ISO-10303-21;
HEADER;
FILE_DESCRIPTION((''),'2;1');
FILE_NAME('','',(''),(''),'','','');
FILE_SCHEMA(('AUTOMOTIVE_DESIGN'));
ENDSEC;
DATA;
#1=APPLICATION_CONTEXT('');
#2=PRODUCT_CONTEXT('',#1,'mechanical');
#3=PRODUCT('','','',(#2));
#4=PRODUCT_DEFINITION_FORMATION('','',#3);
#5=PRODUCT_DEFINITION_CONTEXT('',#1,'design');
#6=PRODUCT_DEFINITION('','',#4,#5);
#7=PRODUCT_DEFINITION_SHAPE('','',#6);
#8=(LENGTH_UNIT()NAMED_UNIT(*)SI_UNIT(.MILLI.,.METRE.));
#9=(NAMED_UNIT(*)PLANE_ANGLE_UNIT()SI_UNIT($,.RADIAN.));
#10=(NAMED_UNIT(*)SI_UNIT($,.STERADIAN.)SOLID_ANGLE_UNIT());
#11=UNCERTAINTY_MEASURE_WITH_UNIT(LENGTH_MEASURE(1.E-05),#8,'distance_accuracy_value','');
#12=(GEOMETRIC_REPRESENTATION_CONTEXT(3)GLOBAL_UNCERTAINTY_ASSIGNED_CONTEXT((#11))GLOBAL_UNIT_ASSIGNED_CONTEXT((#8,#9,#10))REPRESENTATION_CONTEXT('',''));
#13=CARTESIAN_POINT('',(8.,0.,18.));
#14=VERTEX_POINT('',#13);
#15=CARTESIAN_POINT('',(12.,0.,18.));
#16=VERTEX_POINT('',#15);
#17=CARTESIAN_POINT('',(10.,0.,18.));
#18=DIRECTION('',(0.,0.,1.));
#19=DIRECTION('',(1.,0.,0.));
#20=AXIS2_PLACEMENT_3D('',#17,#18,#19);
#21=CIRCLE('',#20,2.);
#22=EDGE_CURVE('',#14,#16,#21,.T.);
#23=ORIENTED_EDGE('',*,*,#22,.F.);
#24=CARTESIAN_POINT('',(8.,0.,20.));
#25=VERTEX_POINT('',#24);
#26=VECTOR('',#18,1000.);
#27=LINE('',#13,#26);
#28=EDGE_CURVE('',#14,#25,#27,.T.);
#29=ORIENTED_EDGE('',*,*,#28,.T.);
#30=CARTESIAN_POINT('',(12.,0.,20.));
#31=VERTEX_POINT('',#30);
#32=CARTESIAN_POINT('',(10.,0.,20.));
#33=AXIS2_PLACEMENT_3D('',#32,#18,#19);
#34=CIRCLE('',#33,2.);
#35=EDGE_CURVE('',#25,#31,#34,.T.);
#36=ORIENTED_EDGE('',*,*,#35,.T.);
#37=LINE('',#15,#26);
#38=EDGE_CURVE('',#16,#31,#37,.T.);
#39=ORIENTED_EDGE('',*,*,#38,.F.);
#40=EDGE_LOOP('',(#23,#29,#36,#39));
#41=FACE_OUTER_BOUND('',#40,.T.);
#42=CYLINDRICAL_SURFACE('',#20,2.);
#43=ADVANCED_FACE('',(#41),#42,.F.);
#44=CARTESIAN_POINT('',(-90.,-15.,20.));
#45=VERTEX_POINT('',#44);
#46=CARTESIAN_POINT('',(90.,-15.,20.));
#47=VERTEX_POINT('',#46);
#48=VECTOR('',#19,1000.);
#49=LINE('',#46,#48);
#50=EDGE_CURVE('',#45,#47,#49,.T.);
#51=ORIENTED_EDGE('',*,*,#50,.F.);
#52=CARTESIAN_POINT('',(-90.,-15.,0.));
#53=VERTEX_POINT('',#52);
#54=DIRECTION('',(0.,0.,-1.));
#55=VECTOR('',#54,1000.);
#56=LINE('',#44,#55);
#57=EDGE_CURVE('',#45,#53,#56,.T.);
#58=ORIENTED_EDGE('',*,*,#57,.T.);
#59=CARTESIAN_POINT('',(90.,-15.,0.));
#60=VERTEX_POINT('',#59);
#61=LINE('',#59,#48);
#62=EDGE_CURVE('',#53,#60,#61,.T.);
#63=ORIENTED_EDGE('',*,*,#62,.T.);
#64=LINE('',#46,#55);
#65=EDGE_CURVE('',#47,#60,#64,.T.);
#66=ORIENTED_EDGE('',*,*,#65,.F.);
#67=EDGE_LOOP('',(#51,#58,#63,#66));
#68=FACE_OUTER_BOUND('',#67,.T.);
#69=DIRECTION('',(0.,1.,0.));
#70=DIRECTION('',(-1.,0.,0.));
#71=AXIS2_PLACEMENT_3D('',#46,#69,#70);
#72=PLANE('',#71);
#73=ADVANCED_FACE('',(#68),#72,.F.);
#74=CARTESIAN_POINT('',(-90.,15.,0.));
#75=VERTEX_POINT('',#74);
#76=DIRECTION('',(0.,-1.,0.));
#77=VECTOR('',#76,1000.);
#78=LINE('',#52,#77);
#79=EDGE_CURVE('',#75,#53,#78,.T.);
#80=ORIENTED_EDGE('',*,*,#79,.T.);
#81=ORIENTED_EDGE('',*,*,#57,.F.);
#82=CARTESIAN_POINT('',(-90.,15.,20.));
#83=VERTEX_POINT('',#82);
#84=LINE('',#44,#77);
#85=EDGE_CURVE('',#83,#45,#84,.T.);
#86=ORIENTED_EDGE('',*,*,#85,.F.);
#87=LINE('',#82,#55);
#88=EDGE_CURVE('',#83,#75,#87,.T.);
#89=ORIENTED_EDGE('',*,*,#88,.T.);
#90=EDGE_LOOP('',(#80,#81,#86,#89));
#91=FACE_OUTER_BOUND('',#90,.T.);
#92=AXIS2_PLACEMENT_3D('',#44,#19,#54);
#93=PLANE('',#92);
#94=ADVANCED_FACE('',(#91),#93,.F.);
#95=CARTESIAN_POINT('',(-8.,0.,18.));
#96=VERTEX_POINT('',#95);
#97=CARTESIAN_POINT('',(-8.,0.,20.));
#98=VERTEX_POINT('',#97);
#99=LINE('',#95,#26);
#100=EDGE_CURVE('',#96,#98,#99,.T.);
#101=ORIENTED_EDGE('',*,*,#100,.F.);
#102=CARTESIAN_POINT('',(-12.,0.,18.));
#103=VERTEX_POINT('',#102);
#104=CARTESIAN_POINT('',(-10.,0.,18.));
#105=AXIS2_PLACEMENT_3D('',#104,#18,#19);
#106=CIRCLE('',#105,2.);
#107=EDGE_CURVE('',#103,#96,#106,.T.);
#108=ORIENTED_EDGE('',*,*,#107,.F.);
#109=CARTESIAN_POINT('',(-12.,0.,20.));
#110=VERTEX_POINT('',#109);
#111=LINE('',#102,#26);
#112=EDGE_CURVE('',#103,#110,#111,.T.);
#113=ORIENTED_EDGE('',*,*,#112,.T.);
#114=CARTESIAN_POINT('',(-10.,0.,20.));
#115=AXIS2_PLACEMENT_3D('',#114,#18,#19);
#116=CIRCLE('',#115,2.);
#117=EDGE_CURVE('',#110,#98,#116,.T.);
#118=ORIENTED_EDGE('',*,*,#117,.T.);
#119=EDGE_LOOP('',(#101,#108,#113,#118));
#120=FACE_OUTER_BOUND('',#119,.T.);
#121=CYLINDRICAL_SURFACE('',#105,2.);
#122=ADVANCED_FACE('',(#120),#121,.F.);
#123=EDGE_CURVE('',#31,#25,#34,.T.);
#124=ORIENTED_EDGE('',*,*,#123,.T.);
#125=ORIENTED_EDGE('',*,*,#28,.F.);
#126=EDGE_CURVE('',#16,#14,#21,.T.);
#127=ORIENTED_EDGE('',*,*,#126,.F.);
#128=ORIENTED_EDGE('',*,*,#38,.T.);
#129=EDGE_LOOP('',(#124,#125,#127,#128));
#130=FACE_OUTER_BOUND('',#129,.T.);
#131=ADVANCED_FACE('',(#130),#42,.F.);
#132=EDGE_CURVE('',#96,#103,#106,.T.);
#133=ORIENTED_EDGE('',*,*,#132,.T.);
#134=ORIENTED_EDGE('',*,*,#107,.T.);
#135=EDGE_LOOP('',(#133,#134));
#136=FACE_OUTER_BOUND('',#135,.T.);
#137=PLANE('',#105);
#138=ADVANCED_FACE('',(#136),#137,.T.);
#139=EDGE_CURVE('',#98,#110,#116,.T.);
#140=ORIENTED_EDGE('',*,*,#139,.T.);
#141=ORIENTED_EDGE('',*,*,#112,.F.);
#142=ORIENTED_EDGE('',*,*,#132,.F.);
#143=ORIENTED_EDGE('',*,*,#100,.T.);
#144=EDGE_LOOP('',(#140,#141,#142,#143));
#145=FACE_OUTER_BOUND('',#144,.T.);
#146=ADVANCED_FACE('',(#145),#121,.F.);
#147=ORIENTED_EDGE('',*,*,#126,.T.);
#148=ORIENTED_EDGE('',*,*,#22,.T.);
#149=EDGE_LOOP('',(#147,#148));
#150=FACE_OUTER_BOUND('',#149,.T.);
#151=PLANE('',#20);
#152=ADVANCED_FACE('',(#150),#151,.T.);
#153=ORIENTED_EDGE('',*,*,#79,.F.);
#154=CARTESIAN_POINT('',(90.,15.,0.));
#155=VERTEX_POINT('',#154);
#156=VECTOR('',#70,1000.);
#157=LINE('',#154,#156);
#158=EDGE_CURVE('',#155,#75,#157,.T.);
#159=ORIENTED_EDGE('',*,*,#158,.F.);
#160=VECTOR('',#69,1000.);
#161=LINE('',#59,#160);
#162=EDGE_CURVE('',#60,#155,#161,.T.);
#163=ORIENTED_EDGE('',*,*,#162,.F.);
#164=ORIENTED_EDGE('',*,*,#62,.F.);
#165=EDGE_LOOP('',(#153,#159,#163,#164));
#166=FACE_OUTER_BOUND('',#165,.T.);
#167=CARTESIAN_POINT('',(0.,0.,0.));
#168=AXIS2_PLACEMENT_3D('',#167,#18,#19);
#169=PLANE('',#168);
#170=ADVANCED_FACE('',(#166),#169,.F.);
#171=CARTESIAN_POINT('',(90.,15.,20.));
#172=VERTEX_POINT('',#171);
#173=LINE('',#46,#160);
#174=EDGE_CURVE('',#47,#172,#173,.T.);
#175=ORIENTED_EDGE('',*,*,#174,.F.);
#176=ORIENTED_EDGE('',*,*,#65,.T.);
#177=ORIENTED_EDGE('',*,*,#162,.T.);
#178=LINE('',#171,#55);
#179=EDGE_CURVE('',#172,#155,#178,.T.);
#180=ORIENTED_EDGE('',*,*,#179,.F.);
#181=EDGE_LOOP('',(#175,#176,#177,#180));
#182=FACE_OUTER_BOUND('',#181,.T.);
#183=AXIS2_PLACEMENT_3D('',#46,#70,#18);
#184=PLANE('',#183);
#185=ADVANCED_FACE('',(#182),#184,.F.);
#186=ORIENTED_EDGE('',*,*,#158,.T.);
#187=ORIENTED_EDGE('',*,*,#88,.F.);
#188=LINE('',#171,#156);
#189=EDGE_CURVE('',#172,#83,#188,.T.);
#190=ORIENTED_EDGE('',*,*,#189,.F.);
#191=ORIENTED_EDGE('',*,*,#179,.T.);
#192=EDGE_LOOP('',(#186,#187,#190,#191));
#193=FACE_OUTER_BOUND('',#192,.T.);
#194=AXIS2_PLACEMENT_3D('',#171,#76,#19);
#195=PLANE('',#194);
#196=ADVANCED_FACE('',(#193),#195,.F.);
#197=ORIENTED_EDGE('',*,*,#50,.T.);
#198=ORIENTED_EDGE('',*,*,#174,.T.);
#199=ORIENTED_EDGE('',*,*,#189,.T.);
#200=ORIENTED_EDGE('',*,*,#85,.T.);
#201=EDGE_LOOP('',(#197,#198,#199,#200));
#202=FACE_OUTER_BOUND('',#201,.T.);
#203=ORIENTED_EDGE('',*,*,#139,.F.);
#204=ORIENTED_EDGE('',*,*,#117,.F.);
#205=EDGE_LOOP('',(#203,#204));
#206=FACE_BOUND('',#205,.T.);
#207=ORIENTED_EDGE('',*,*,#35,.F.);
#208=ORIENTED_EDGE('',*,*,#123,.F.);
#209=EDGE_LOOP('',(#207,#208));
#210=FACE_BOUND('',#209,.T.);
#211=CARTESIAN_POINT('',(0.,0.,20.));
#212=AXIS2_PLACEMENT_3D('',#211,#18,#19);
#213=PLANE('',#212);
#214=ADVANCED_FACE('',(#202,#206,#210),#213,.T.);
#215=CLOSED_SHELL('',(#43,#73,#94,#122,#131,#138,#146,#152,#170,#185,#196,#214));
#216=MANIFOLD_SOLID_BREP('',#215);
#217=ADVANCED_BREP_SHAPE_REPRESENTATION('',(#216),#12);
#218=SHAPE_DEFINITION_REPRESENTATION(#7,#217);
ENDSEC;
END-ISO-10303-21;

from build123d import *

# Parameters (mm, degrees)
SKETCH_1_W          = 180
SKETCH_1_H          = 30
EXTRUDE_1_DEPTH     = 20
SKETCH_2_R          = 2
CUT_EXTRUDE_1_DEPTH = 2


with BuildPart() as part:
    # 草图1 → 凸台-拉伸1 (new body)
    with BuildSketch(Plane.XY):
        Rectangle(SKETCH_1_W, SKETCH_1_H)
    extrude(amount=EXTRUDE_1_DEPTH)

    # 草图2 → 切除-拉伸1 (cut)
    with BuildSketch(Plane.XY.offset(20)):
        with Locations((-10, 0)):
            Circle(SKETCH_2_R)
        with Locations((10, 0)):
            Circle(SKETCH_2_R)
    extrude(amount=-CUT_EXTRUDE_1_DEPTH, mode=Mode.SUBTRACT)


solid = part.part
